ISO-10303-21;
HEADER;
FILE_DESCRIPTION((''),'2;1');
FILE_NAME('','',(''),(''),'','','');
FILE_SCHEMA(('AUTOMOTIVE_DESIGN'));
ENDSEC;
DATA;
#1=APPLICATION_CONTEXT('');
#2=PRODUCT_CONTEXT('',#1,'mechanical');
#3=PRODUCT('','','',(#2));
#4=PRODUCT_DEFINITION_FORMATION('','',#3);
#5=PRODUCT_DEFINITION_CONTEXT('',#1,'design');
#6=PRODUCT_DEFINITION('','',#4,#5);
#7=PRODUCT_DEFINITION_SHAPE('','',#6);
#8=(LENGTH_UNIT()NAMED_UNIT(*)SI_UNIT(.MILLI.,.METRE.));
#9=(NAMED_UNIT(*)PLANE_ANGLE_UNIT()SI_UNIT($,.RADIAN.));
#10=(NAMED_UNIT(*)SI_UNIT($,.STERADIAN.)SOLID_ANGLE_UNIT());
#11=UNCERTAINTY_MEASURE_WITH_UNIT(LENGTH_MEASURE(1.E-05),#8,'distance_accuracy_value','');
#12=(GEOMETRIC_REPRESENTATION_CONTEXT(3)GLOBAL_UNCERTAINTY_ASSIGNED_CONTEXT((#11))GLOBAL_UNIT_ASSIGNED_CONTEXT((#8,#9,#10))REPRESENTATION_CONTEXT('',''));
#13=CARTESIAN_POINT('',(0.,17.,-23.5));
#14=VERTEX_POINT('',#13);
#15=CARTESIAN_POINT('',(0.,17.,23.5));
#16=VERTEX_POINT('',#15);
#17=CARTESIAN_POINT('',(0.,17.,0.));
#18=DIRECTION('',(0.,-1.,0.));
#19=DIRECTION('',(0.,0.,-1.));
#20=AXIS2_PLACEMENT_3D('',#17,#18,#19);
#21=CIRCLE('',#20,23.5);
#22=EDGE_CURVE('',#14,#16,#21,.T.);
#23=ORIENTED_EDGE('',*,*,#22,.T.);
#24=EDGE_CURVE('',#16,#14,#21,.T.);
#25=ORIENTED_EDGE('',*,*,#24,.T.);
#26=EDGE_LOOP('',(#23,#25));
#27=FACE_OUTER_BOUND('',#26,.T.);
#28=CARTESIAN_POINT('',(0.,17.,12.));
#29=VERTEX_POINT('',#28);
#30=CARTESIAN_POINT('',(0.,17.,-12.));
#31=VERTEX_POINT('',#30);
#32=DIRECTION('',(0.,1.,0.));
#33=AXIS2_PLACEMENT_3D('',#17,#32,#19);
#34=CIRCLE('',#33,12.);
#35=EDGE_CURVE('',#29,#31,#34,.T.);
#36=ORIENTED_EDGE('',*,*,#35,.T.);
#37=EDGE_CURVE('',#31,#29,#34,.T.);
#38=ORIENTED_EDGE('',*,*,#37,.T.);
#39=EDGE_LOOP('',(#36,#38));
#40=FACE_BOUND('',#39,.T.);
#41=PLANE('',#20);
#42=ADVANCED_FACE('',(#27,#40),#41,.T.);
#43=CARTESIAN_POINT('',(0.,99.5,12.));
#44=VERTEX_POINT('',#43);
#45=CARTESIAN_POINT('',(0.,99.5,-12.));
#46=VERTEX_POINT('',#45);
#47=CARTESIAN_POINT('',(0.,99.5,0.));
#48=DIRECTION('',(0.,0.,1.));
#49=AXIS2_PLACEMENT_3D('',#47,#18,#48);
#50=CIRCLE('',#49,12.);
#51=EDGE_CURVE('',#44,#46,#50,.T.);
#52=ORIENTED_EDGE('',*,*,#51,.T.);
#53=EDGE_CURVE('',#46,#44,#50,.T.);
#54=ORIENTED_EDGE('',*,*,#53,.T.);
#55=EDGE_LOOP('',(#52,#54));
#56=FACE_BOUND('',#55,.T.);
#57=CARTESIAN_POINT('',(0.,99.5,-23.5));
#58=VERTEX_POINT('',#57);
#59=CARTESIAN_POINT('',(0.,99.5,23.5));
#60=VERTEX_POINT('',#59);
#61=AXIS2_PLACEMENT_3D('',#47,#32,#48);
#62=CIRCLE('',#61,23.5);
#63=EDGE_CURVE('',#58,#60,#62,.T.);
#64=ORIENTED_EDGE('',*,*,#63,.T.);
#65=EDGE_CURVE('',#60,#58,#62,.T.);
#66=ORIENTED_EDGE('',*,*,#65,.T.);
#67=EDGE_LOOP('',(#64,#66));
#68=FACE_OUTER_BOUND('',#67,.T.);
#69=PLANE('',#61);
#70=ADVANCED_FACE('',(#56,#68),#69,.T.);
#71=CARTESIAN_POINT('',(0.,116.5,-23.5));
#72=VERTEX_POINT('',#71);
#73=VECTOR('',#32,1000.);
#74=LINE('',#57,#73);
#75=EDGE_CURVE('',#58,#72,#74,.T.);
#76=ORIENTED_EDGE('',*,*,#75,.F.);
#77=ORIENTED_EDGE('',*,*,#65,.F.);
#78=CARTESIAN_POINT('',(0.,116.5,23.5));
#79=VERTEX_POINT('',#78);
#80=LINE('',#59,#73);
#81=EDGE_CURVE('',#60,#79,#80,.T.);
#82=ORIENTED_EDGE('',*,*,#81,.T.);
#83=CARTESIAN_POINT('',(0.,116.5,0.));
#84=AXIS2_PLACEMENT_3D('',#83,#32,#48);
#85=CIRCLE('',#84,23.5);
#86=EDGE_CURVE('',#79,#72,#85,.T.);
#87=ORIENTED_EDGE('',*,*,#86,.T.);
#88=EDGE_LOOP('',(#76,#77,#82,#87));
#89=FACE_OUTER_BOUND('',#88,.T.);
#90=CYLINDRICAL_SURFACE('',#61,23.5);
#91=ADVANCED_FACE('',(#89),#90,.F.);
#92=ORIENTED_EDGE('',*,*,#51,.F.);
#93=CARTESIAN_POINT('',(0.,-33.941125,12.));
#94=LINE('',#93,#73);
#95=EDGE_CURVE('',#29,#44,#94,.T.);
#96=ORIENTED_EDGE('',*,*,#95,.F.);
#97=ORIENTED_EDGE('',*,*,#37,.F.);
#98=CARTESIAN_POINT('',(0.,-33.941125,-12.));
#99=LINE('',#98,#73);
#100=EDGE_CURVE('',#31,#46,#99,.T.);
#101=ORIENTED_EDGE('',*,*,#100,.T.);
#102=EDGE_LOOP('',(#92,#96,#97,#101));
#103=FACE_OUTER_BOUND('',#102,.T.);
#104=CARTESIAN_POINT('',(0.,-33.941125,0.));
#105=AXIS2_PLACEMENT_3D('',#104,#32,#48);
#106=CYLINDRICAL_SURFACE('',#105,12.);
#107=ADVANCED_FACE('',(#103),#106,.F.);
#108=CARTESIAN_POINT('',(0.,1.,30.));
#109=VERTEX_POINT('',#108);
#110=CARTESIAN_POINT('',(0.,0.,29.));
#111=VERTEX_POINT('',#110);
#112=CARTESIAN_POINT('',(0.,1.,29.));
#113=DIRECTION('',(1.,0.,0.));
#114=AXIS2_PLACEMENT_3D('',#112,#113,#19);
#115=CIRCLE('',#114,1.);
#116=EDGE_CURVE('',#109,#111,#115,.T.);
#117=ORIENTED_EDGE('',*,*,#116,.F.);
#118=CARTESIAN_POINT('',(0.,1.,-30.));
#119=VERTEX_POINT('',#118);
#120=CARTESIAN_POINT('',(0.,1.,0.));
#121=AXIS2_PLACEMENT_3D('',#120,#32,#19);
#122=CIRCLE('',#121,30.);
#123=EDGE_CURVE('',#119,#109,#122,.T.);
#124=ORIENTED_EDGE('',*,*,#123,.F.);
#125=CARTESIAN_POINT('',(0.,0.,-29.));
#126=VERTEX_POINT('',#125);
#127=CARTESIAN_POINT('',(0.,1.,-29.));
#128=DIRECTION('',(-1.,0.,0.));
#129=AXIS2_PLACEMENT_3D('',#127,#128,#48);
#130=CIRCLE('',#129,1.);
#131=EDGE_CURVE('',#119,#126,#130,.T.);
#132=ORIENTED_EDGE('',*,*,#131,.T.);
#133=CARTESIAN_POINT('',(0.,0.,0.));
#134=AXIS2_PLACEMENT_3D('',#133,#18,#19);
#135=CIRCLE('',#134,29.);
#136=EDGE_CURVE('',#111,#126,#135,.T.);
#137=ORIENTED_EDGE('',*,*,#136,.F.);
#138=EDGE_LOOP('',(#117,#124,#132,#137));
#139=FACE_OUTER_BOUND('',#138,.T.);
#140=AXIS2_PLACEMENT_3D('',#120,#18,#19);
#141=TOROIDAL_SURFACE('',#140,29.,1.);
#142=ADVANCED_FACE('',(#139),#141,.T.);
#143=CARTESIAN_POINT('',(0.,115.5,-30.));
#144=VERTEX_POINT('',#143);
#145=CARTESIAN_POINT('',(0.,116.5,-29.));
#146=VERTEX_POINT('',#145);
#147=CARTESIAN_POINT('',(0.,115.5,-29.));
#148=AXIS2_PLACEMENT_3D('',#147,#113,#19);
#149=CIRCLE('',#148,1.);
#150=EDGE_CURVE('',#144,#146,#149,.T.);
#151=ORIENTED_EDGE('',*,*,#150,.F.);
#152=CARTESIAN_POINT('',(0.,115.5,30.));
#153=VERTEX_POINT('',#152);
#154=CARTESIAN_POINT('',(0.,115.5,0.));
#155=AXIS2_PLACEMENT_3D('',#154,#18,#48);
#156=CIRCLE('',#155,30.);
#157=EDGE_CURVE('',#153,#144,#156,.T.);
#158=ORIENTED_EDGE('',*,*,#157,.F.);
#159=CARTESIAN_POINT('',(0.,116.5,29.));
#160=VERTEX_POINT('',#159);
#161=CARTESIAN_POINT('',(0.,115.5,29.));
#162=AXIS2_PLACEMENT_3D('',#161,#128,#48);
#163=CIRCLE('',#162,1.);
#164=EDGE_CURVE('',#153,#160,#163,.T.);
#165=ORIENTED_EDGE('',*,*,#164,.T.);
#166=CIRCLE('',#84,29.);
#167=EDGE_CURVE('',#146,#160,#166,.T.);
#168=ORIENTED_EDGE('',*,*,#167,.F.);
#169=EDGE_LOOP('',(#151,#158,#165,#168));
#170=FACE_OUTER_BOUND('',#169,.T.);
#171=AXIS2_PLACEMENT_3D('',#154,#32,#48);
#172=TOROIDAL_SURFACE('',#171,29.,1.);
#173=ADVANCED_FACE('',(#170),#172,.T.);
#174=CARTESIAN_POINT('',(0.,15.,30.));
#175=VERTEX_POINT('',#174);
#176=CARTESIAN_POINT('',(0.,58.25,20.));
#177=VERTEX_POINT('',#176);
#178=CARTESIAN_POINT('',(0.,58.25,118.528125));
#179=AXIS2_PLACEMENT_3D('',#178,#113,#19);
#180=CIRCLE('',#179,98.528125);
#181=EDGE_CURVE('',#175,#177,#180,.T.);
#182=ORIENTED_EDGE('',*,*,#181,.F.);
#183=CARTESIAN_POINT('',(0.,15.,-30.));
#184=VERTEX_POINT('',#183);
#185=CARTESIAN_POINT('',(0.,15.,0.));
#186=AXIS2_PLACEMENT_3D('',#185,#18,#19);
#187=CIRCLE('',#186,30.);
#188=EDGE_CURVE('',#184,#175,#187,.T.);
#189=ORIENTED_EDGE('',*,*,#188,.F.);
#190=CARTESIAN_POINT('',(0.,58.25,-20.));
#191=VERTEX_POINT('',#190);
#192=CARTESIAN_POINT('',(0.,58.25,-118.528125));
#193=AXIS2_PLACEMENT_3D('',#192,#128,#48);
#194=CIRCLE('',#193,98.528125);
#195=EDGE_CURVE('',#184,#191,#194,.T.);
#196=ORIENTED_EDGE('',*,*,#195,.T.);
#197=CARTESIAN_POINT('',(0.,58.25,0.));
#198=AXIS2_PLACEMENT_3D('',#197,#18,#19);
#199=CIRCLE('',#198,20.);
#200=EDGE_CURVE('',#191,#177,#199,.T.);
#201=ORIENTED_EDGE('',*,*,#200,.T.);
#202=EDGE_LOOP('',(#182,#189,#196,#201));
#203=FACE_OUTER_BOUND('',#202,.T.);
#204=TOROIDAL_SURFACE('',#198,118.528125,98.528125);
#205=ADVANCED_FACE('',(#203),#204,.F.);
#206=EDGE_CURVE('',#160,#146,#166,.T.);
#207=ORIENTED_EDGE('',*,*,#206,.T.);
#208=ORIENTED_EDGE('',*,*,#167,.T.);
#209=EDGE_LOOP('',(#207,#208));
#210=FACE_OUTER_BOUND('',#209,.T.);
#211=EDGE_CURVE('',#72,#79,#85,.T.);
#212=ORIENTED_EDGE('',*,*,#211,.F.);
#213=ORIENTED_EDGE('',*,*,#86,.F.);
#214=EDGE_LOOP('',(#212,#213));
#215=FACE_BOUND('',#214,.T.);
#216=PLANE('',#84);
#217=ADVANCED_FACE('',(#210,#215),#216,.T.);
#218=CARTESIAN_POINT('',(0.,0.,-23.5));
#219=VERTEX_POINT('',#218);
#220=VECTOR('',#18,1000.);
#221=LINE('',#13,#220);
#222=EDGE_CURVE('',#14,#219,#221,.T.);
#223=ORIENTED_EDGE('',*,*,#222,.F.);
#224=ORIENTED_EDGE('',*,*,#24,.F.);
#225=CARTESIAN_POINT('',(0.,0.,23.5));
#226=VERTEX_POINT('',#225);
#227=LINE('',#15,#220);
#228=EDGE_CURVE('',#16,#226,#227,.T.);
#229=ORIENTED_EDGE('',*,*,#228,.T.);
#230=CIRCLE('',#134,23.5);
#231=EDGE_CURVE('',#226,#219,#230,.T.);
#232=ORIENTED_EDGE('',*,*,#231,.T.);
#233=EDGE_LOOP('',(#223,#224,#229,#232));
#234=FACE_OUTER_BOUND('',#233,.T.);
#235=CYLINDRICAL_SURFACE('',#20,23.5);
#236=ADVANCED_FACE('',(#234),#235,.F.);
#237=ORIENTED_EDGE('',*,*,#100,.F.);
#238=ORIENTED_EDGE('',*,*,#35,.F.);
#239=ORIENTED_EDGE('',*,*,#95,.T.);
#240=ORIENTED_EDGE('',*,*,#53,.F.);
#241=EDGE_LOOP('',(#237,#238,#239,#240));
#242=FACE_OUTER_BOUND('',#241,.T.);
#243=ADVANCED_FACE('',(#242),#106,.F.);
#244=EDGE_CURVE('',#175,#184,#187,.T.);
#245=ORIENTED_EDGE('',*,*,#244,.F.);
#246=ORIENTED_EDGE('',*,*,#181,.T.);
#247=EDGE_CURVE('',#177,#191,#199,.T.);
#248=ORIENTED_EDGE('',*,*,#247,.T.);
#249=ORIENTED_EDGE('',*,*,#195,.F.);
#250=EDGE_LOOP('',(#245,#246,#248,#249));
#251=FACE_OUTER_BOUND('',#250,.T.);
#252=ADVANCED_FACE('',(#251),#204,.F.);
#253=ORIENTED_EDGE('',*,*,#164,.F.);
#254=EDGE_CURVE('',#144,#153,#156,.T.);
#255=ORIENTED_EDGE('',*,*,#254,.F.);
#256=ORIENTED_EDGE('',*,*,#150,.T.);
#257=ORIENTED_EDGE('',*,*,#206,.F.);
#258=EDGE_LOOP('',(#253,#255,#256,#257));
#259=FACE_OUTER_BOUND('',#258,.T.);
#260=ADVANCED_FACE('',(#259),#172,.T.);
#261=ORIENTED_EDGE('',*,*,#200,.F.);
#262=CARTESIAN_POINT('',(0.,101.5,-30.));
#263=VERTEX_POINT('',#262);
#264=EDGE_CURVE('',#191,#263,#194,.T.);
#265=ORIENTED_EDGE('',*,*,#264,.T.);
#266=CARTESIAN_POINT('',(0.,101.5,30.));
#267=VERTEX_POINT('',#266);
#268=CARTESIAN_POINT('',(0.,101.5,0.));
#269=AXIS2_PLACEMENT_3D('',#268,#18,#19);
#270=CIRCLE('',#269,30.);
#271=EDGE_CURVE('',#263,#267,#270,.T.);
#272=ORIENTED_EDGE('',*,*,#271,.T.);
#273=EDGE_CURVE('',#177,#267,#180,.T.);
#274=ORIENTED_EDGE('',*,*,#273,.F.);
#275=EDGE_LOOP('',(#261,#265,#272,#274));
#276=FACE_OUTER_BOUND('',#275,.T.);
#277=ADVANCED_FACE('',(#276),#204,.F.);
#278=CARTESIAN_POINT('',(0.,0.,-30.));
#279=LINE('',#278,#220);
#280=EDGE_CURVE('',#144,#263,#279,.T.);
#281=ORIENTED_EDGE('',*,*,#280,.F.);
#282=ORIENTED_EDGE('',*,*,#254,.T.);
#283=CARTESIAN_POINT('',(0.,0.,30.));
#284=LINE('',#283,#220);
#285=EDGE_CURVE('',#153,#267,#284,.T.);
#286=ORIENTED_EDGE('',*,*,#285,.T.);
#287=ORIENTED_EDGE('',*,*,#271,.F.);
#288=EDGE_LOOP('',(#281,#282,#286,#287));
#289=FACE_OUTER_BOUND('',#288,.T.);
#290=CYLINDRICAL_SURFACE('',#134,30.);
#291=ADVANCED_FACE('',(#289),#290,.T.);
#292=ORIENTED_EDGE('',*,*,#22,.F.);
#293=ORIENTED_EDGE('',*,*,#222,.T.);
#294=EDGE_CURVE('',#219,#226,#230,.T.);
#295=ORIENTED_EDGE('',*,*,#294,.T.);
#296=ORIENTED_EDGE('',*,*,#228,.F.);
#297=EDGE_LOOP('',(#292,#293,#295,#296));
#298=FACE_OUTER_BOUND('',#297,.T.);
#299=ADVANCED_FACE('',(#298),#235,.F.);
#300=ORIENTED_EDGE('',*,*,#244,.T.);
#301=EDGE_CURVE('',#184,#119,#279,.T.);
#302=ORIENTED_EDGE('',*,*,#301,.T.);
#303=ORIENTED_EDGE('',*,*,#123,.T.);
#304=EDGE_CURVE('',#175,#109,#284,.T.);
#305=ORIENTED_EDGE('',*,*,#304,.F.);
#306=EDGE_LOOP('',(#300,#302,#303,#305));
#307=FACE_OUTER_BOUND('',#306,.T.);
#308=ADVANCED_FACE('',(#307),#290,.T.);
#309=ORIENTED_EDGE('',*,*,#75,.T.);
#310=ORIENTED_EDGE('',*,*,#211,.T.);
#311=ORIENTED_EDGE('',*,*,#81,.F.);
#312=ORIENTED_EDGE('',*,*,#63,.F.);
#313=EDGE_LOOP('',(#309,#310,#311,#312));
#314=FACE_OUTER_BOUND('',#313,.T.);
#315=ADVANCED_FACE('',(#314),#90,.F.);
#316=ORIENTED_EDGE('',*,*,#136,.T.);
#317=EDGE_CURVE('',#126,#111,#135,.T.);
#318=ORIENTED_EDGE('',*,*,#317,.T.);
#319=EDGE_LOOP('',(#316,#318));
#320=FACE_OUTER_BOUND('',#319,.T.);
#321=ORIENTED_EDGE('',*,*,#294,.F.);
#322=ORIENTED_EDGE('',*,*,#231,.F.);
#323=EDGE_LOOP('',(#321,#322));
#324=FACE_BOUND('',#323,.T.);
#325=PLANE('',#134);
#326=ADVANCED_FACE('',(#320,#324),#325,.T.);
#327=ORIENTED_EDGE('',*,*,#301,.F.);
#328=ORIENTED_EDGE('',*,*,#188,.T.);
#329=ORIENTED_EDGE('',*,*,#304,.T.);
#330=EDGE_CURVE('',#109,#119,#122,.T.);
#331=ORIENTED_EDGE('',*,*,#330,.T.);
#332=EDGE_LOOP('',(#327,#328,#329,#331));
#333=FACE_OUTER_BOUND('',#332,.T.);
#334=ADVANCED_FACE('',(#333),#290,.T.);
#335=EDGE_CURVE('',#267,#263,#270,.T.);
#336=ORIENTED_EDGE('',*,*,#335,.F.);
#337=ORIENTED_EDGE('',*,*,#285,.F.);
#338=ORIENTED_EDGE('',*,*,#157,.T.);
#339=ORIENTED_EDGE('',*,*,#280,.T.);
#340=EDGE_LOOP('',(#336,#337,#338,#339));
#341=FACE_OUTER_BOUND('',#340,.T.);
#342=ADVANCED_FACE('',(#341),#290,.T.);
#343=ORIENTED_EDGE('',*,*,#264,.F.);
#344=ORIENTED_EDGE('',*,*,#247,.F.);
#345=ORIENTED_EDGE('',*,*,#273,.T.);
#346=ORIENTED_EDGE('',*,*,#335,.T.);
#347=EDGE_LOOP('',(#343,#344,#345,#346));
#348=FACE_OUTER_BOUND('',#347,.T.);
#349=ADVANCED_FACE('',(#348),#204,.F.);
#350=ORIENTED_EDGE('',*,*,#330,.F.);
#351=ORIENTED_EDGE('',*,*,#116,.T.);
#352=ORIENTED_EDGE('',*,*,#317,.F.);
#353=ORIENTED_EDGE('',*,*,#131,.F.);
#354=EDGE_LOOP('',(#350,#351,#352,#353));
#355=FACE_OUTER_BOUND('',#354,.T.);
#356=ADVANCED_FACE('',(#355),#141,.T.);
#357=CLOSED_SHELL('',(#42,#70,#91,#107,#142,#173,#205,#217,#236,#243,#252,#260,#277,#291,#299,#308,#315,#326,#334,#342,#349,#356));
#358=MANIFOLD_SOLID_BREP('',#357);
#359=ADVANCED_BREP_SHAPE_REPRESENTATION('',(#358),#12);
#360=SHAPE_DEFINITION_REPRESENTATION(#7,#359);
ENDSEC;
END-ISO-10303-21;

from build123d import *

# Parameters (mm, degrees)
SKETCH_2_R          = 12
CUT_EXTRUDE_1_DEPTH = 116.5
SKETCH_3_R          = 23.5
SKETCH_3_R_2        = 10
CUT_EXTRUDE_2_DEPTH = 17
CUT_EXTRUDE_START   = -17
SKETCH_4_R          = 23.5
SKETCH_4_R_2        = 10
CUT_EXTRUDE_3_DEPTH = 17
FILLET_1_R          = 1


with BuildPart() as part:
    # 草图1 → 旋转1 (revolve)
    with BuildSketch(Plane.XY, mode=Mode.PRIVATE) as revolve_1_sk:
        with BuildLine():
            Line((0, 0), (0, 116.5))
            Line((0, 116.5), (30, 116.5))
            Line((30, 116.5), (30, 101.5))
            ThreePointArc((30, 101.5), (20, 58.25), (30, 15))
            Line((30, 15), (30, 0))
            Line((30, 0), (0, 0))
        make_face()
    revolve(revolve_1_sk.sketch.rotate(Axis((0, 0, 0), (0, 1, 0)), 90), axis=Axis((0, 0, 0), (0, 1, 0)))

    # 草图2 → 切除-拉伸1 (cut)
    with BuildSketch(Plane(origin=(0, 116.5, 0), x_dir=(1, 0, 0), z_dir=(0, 1, 0))):
        with Locations(Location((0, 0, 0), (0, 0, 270))):
            Circle(SKETCH_2_R)
    extrude(amount=-CUT_EXTRUDE_1_DEPTH, mode=Mode.SUBTRACT)

    # 草图3 → 切除-拉伸2 (cut)
    with BuildSketch(Plane(origin=(0, 116.5, 0), x_dir=(1, 0, 0), z_dir=(0, 1, 0))):
        with Locations(Location((0, 0, 0), (0, 0, 270))):
            Circle(SKETCH_3_R)
        Circle(SKETCH_3_R_2, mode=Mode.SUBTRACT)
    extrude(amount=-CUT_EXTRUDE_2_DEPTH, mode=Mode.SUBTRACT)

    # 草图4 → 切除-拉伸3 (cut)
    with BuildSketch(Plane.XZ.offset(CUT_EXTRUDE_START)):
        with Locations(Location((0, 0, 0), (0, 0, 90))):
            Circle(SKETCH_4_R)
        Circle(SKETCH_4_R_2, mode=Mode.SUBTRACT)
    extrude(amount=CUT_EXTRUDE_3_DEPTH, mode=Mode.SUBTRACT)

    # 圆角1
    fillet_1_edges = [part.edges().sort_by_distance(p)[0] for p in [
        (0, 116.5, 30),
        (0, 0, 30),
    ]]
    fillet(fillet_1_edges, radius=FILLET_1_R)


solid = part.part
